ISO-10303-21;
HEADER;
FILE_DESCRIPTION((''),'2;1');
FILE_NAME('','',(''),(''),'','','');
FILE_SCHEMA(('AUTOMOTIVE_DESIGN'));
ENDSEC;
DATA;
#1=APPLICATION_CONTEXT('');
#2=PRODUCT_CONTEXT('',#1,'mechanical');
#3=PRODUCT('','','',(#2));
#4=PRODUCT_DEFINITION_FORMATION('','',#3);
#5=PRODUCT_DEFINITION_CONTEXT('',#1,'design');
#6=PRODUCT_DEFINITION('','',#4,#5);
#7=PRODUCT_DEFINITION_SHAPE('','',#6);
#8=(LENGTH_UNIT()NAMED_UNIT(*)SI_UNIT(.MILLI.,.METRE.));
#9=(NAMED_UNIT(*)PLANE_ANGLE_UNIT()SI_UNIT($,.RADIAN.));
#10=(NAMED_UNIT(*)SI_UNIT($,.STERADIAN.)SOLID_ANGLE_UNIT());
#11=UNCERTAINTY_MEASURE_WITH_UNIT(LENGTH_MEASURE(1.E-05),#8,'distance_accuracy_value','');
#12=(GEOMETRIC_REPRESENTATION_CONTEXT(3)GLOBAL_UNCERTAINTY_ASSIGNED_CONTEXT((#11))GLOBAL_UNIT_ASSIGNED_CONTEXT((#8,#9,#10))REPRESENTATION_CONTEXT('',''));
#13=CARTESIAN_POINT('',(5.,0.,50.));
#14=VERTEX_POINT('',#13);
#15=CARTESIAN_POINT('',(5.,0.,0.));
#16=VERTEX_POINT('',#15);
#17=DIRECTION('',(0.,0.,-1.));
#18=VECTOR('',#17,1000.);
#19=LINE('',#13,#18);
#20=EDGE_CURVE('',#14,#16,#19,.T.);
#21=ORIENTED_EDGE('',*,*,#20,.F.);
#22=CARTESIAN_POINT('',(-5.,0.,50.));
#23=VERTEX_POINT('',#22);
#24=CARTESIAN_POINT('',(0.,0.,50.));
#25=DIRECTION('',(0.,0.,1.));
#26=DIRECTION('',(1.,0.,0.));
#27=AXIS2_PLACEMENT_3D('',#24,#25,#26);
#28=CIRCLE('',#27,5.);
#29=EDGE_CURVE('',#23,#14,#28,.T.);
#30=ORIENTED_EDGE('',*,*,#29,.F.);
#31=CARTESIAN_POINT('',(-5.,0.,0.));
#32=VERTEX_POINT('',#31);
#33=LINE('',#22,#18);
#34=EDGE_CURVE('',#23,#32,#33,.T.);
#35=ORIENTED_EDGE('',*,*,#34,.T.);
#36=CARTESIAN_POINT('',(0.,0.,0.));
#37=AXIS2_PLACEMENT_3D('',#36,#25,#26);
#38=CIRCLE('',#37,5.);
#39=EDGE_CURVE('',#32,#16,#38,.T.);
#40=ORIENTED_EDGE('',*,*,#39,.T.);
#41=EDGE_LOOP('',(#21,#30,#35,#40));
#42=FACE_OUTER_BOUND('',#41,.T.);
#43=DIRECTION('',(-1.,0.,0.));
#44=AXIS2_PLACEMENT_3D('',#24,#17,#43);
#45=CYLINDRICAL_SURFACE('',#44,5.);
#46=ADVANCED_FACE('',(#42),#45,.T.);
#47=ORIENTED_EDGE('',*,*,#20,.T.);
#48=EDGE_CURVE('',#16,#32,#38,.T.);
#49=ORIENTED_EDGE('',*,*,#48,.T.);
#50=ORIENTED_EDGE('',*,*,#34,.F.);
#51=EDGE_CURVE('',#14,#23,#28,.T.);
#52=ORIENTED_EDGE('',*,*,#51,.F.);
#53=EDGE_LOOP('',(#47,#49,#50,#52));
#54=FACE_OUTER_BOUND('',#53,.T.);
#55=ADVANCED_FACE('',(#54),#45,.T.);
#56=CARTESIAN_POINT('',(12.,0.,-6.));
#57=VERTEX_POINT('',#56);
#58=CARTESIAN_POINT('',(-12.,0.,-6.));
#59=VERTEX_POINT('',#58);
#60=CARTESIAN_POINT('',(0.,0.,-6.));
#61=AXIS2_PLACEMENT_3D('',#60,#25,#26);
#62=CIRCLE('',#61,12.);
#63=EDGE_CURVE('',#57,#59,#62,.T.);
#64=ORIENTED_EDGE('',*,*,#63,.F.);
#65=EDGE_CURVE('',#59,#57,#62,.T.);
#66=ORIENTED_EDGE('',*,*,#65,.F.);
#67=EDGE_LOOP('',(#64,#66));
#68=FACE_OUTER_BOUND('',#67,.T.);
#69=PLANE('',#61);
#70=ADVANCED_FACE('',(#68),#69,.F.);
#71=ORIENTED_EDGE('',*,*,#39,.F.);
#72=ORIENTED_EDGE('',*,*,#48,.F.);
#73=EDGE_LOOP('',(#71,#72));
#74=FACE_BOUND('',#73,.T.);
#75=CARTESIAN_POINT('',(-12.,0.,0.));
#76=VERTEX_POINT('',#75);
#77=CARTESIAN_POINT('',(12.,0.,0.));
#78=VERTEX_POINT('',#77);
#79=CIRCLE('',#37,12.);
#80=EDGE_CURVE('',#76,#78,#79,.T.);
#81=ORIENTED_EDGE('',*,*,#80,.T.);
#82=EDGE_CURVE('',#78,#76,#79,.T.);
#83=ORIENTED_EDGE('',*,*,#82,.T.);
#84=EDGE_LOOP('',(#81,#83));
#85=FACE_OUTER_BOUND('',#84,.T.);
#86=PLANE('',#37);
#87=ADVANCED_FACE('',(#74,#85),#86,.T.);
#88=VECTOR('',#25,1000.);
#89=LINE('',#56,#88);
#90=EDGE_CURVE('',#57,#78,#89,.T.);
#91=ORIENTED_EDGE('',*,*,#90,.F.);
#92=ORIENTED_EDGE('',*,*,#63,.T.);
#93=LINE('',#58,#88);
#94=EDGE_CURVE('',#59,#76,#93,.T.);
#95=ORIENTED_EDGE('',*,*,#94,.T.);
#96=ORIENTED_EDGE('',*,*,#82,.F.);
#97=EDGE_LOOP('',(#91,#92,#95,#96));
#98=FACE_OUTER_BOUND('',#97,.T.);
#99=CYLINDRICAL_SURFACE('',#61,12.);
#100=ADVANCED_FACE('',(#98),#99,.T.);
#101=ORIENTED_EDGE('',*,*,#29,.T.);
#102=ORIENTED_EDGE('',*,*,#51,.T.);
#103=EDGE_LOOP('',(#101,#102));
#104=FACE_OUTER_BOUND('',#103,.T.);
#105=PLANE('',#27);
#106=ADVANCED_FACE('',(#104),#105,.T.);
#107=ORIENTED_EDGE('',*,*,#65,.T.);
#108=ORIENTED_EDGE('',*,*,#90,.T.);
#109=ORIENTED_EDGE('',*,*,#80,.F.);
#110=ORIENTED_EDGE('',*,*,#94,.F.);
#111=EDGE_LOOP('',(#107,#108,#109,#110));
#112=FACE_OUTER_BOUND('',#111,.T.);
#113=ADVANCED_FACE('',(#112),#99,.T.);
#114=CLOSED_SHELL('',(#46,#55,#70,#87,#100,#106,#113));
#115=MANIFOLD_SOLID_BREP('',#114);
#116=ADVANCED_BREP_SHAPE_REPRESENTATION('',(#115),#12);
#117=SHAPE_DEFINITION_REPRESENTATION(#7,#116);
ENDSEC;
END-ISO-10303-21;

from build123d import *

# Parameters (mm, degrees)
SKETCH_1_R      = 5
EXTRUDE_1_DEPTH = 50
SKETCH_2_R      = 12
EXTRUDE_2_DEPTH = 6


with BuildPart() as part:
    # 草图1 → 凸台-拉伸1 (new body)
    with BuildSketch(Plane.XY):
        Circle(SKETCH_1_R)
    extrude(amount=EXTRUDE_1_DEPTH)

    # 草图2 → 凸台-拉伸2 (add)
    with BuildSketch(Plane.XY):
        Circle(SKETCH_2_R)
    extrude(amount=-EXTRUDE_2_DEPTH)


solid = part.part
